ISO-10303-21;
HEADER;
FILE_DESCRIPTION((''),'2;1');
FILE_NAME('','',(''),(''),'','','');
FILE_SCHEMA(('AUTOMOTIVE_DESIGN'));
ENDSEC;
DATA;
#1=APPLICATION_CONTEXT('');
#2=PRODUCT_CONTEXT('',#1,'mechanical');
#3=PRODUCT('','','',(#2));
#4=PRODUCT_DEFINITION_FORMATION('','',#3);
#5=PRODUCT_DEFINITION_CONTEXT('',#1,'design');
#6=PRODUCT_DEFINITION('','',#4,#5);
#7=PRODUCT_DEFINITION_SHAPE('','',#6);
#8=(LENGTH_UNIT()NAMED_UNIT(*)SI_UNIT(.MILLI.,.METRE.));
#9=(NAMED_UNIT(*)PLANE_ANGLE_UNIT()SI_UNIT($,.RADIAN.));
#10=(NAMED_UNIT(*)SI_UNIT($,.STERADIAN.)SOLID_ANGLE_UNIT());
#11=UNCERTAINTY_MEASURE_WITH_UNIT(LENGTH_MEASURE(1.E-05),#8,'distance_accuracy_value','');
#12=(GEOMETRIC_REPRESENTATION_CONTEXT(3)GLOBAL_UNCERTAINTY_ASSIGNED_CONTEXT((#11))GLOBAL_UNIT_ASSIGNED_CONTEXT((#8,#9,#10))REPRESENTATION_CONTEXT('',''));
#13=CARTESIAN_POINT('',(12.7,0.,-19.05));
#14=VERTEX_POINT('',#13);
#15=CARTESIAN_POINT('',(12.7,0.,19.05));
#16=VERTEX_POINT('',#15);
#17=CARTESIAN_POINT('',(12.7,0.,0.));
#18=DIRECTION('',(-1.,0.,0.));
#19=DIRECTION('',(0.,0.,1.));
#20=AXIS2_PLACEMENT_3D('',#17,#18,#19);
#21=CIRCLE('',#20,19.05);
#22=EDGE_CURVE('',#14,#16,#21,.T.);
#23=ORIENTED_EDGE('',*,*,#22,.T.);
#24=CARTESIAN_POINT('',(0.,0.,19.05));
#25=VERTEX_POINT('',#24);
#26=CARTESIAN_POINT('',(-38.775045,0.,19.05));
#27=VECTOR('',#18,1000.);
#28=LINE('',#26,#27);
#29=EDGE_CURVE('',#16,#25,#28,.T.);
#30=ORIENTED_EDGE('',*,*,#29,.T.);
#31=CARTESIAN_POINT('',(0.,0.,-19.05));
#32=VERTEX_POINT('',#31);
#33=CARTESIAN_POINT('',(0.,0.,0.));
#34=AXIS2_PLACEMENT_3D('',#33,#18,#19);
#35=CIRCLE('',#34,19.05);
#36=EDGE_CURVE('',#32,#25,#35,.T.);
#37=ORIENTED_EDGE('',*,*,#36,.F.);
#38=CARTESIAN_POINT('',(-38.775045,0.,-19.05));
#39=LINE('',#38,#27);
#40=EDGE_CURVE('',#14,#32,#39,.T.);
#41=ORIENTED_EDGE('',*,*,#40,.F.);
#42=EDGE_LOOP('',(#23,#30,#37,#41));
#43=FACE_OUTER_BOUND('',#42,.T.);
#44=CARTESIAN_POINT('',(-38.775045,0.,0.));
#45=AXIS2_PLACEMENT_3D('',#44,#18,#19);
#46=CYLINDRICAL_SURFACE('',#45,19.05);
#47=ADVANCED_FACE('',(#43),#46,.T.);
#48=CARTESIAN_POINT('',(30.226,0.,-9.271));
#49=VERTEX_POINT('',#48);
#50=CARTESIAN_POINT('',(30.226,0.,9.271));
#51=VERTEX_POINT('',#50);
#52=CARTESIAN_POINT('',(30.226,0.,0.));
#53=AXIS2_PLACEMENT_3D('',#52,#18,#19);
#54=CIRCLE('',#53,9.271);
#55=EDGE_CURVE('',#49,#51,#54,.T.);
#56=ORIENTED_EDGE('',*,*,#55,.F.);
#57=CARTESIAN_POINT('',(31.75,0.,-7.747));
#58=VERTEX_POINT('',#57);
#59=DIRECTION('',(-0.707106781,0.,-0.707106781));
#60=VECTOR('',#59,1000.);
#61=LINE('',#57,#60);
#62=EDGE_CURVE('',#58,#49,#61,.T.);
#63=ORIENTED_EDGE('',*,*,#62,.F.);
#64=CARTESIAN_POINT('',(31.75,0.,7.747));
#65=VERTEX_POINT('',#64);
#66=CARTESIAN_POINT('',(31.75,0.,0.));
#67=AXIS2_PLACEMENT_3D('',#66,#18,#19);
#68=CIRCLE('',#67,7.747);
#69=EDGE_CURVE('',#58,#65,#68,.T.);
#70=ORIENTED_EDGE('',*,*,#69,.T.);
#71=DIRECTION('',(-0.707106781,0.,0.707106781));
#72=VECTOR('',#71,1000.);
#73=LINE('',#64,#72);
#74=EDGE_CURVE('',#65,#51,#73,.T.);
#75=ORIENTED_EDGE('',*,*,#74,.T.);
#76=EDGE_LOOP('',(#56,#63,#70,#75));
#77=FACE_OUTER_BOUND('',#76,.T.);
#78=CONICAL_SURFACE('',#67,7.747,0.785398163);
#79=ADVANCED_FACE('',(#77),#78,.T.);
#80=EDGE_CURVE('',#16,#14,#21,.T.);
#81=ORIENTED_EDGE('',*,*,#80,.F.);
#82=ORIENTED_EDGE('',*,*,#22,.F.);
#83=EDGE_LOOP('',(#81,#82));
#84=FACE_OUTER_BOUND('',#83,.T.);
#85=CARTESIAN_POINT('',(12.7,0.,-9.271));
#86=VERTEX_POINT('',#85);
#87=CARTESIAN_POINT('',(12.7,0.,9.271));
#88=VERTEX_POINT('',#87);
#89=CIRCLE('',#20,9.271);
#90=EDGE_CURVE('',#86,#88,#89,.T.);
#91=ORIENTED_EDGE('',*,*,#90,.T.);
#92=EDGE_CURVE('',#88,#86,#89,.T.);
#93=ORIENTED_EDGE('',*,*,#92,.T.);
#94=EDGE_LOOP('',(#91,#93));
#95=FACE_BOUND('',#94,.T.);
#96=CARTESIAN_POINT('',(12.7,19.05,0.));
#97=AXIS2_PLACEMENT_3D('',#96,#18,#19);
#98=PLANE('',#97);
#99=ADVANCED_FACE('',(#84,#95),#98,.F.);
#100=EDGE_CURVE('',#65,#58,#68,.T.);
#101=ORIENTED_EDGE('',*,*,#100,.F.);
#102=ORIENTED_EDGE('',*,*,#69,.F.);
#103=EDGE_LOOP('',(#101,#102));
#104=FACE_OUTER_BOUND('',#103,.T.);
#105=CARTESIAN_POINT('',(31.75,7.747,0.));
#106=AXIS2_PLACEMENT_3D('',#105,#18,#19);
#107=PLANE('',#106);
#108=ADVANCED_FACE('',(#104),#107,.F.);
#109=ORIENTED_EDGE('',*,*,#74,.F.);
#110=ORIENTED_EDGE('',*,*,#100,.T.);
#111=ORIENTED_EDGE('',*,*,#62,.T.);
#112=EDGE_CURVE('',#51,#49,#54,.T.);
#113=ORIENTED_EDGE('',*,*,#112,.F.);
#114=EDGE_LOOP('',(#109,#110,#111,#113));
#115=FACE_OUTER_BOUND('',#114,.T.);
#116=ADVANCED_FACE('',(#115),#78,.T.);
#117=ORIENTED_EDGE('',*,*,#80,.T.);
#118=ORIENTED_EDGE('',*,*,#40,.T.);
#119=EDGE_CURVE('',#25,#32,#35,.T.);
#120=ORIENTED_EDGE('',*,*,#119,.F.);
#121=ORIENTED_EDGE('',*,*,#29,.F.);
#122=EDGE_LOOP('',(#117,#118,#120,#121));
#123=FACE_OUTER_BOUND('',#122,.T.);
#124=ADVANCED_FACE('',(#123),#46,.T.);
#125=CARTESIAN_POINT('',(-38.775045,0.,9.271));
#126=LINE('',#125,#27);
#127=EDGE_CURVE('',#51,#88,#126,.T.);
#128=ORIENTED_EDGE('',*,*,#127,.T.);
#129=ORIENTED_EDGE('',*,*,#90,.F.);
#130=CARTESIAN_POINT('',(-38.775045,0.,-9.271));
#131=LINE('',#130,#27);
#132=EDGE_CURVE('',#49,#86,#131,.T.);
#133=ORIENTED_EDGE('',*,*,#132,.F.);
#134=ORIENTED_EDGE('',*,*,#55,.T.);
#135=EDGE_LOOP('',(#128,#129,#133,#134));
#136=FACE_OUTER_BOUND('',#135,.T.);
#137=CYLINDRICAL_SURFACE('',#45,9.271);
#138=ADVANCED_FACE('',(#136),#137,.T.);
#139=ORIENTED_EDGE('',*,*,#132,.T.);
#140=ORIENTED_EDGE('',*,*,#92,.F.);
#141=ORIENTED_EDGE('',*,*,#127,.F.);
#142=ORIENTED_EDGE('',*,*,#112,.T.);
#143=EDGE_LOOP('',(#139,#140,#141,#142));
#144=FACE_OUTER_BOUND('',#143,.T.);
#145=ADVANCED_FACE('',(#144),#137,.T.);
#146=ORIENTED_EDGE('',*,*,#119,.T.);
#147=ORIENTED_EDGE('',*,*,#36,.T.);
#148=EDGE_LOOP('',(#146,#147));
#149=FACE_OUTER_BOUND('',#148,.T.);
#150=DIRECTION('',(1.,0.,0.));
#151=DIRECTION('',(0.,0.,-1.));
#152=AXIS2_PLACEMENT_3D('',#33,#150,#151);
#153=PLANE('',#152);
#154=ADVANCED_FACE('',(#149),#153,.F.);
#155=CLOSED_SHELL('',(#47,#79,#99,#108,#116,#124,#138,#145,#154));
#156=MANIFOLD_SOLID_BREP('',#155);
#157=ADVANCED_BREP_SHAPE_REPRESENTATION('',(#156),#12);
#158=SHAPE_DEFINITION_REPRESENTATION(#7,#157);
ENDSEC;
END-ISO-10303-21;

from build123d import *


with BuildPart() as part:
    # Sketch1 → Revolve1 (revolve)
    with BuildSketch(Plane.XY, mode=Mode.PRIVATE) as revolve1_sk:
        Polygon((0, 0), (0, 19.05), (12.7, 19.05), (12.7, 9.271), (30.226, 9.271), (31.75, 7.747), (31.75, 0), align=None)
    revolve(revolve1_sk.sketch.rotate(Axis((-38.775045045, 0, 0), (1, 0, 0)), 90), axis=Axis((-38.775045045, 0, 0), (1, 0, 0)))


solid = part.part
